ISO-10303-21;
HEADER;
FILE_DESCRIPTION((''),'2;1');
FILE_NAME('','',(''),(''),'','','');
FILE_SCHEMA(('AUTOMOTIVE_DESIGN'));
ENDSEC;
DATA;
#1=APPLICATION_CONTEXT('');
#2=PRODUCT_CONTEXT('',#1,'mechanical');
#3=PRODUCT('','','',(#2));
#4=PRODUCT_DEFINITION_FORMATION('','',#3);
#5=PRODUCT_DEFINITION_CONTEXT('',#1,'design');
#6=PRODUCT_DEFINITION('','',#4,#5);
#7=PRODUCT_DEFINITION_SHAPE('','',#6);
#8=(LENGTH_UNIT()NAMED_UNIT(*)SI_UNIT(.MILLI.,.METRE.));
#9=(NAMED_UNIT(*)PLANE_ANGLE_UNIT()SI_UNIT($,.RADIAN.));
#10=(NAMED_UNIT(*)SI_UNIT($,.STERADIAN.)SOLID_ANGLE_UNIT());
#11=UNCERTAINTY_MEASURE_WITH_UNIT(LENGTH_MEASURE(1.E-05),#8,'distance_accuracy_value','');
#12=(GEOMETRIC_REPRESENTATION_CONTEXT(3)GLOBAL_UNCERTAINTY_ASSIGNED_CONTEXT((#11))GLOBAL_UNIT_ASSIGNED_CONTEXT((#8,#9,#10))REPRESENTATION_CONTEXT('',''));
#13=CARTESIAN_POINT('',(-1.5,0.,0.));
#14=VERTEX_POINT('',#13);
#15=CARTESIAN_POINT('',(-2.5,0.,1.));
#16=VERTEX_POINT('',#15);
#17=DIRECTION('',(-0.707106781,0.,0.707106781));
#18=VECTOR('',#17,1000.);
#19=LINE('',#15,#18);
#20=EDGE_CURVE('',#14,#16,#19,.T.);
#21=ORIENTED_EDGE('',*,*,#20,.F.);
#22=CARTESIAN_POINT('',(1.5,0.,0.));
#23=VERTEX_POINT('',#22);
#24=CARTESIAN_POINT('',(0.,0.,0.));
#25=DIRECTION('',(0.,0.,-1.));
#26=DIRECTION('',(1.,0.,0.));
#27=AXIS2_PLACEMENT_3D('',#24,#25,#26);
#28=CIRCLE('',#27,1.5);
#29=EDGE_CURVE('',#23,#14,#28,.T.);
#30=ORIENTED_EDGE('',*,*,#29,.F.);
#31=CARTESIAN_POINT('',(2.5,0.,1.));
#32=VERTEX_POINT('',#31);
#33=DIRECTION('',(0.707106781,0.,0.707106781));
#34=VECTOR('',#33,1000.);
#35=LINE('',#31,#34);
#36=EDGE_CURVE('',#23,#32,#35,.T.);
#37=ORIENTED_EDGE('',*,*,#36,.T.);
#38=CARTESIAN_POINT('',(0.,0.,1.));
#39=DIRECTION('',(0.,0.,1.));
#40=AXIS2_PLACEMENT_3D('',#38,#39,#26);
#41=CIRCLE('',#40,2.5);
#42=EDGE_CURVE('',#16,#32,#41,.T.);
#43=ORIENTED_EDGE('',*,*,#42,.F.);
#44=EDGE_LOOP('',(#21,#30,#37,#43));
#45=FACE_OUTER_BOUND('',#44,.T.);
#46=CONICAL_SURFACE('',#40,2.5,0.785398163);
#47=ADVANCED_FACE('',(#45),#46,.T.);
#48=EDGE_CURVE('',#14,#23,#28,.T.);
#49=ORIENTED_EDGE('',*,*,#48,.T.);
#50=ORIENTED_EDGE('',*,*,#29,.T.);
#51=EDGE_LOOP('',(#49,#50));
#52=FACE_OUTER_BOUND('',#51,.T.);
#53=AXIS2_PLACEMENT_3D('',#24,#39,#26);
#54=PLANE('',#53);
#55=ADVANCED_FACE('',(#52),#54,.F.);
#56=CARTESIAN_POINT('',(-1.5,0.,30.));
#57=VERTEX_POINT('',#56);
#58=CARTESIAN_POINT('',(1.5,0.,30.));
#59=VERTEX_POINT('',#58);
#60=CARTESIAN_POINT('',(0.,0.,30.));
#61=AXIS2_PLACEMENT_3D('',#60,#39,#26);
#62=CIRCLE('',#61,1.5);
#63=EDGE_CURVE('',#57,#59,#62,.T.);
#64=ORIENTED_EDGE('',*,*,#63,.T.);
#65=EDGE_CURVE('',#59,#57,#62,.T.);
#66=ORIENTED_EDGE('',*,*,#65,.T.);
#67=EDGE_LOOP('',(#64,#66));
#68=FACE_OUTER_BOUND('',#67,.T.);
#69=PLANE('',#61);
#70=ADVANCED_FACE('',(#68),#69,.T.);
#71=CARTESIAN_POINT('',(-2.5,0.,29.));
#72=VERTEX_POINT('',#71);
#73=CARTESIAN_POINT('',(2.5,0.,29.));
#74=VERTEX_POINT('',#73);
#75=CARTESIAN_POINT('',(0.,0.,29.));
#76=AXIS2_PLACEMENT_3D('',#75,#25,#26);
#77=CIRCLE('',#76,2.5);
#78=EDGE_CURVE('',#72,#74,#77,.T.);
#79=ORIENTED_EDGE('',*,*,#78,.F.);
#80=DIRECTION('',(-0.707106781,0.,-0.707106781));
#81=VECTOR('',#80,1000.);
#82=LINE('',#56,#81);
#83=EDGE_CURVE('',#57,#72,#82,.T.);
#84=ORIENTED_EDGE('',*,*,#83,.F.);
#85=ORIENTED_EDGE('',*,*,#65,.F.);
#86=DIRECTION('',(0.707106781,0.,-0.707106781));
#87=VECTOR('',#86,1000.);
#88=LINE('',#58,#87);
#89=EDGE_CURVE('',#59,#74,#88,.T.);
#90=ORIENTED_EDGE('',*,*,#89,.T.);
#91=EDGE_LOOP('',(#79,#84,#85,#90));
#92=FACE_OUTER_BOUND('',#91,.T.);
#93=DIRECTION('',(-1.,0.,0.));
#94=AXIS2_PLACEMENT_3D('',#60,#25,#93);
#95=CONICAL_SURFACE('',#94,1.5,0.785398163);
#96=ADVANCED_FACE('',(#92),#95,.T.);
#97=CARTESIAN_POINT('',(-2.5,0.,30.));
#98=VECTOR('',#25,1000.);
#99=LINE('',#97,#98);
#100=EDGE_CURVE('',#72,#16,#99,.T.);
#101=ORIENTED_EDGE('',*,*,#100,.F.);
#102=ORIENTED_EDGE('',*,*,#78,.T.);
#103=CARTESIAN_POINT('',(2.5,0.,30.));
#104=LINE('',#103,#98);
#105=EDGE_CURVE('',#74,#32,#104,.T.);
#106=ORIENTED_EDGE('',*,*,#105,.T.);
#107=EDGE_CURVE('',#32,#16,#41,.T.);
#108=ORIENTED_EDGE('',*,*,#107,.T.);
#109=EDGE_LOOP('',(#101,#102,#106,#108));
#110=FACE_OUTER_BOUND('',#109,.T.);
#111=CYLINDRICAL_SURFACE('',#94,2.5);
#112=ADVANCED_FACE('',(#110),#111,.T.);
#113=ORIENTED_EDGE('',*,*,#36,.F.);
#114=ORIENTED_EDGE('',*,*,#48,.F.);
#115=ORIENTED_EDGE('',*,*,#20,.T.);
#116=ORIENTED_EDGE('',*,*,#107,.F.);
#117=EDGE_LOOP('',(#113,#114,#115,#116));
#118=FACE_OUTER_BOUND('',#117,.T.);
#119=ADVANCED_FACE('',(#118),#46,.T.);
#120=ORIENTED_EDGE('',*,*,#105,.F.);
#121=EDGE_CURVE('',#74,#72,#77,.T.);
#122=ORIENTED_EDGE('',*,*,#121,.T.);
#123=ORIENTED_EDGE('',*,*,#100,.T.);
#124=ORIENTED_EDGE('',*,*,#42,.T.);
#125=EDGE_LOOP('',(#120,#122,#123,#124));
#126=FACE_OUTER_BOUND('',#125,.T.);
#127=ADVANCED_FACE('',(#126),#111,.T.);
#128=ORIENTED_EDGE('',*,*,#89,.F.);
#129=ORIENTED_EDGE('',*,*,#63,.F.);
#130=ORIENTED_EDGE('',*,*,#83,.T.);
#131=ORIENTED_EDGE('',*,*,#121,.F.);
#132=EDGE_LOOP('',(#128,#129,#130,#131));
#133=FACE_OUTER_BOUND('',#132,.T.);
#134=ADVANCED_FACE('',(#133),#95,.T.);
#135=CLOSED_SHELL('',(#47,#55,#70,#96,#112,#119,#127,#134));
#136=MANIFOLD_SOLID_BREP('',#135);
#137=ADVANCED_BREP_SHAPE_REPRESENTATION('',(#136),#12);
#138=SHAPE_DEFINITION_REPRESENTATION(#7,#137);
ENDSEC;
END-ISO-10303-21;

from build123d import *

# Parameters (mm, degrees)
SKETCH1_R           = 2.5
BOSS_EXTRUDE1_DEPTH = 30
CHAMFER1_SIZE       = 1


with BuildPart() as part:
    # Sketch1 → Boss-Extrude1 (new body)
    with BuildSketch(Plane.XY):
        Circle(SKETCH1_R)
    extrude(amount=BOSS_EXTRUDE1_DEPTH)

    # Chamfer1
    chamfer1_edges = [part.edges().sort_by_distance(p)[0] for p in [
        (-2.5, 0, 0),
        (-2.5, 0, 30),
    ]]
    chamfer(chamfer1_edges, length=CHAMFER1_SIZE)


solid = part.part
